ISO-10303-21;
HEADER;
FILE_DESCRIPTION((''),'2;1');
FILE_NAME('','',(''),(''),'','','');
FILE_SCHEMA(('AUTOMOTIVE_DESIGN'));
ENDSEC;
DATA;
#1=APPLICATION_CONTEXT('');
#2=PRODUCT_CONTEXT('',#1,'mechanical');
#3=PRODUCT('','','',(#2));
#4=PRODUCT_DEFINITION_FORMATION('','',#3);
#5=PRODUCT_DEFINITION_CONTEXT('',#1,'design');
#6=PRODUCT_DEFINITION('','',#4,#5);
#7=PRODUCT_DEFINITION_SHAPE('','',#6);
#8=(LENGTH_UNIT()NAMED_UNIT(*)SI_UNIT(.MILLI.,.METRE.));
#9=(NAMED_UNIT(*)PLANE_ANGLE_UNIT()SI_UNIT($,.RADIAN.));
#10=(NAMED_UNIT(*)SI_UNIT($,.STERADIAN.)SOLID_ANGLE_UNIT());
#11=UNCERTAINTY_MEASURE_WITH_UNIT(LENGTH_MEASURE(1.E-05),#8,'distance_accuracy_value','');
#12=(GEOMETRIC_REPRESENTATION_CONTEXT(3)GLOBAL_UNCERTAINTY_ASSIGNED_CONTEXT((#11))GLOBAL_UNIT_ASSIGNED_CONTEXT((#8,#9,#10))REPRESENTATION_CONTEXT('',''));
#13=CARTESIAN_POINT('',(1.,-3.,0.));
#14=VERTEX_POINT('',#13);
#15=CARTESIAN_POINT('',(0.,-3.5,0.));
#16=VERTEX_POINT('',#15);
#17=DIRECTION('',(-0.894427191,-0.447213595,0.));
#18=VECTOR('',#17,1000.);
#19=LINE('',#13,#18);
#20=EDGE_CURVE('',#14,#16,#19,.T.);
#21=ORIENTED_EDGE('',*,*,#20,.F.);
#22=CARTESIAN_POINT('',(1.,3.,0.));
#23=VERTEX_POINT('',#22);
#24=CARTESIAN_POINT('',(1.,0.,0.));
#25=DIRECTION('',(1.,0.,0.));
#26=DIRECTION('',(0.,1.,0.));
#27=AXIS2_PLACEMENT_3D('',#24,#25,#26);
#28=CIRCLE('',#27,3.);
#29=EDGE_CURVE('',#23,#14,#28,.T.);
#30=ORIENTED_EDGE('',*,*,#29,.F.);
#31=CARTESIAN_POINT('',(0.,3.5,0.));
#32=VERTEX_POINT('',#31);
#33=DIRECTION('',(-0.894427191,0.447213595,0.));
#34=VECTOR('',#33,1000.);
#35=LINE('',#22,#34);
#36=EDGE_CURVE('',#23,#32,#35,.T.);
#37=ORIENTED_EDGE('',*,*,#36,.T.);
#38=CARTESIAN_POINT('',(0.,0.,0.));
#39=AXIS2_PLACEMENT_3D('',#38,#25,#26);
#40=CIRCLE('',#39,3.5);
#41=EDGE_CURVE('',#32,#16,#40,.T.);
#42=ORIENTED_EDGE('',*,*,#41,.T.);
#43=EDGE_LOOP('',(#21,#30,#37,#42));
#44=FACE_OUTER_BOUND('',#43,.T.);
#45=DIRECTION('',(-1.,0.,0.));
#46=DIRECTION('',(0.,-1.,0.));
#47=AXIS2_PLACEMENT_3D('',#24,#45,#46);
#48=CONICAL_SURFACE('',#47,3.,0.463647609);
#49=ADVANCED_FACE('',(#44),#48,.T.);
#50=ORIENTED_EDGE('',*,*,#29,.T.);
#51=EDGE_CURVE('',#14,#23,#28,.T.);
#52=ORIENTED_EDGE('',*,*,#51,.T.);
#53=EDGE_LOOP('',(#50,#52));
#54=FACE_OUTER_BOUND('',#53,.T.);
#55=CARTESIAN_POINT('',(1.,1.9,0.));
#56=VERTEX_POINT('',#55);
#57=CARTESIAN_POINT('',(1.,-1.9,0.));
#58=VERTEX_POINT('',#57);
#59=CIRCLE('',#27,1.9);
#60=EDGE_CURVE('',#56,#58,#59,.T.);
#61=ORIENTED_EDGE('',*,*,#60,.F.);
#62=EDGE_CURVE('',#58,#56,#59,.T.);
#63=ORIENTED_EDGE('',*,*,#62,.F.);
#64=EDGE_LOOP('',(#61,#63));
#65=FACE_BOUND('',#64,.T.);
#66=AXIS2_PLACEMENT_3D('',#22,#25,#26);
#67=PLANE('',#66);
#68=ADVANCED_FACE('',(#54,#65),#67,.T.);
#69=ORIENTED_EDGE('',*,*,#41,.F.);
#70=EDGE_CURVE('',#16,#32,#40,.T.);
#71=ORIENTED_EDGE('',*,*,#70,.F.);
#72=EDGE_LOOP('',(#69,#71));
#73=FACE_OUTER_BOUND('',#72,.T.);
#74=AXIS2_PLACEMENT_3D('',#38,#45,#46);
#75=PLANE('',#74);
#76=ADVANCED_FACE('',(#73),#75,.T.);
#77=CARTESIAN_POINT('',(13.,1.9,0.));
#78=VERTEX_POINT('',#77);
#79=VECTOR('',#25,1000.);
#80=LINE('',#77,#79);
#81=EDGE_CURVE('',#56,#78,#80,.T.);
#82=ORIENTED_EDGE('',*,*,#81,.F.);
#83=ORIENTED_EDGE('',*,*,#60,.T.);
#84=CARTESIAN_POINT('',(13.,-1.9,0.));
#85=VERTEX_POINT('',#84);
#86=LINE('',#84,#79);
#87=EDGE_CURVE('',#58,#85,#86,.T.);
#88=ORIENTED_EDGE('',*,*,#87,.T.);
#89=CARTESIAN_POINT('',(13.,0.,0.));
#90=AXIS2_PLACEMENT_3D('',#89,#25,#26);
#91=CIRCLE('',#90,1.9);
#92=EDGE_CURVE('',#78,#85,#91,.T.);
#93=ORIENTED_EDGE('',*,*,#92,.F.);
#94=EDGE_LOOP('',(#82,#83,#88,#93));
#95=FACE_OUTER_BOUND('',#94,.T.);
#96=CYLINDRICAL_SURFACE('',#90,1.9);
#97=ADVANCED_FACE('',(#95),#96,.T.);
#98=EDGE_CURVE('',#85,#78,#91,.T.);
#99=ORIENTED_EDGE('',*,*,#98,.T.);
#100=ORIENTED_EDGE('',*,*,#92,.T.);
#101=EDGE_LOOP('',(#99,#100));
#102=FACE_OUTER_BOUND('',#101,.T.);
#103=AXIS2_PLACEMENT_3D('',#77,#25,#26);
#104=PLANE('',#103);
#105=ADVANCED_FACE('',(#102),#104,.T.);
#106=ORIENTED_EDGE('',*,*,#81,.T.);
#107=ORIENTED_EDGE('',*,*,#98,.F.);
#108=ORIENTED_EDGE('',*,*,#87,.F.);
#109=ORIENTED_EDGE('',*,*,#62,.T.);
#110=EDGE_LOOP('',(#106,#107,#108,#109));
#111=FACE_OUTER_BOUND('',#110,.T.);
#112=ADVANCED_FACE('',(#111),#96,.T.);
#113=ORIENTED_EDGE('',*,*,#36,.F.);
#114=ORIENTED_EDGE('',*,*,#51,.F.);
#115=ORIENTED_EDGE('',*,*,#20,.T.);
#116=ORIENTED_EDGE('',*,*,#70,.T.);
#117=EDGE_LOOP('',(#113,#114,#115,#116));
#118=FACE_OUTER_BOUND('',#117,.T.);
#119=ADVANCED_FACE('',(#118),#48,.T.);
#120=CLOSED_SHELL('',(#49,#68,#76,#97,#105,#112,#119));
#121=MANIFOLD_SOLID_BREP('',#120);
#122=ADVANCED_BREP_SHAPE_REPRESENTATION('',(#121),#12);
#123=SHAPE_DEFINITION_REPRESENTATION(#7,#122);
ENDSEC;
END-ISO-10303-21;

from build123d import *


with BuildPart() as part:
    # Sketch1 → Revolve1 (revolve)
    with BuildSketch(Plane.XY):
        Polygon((0, 0), (0, 3.5), (1, 3), (1, 1.9), (13, 1.9), (13, 0), align=None)
    revolve(axis=Axis((13, 0, 0), (-1, 0, 0)))


solid = part.part
